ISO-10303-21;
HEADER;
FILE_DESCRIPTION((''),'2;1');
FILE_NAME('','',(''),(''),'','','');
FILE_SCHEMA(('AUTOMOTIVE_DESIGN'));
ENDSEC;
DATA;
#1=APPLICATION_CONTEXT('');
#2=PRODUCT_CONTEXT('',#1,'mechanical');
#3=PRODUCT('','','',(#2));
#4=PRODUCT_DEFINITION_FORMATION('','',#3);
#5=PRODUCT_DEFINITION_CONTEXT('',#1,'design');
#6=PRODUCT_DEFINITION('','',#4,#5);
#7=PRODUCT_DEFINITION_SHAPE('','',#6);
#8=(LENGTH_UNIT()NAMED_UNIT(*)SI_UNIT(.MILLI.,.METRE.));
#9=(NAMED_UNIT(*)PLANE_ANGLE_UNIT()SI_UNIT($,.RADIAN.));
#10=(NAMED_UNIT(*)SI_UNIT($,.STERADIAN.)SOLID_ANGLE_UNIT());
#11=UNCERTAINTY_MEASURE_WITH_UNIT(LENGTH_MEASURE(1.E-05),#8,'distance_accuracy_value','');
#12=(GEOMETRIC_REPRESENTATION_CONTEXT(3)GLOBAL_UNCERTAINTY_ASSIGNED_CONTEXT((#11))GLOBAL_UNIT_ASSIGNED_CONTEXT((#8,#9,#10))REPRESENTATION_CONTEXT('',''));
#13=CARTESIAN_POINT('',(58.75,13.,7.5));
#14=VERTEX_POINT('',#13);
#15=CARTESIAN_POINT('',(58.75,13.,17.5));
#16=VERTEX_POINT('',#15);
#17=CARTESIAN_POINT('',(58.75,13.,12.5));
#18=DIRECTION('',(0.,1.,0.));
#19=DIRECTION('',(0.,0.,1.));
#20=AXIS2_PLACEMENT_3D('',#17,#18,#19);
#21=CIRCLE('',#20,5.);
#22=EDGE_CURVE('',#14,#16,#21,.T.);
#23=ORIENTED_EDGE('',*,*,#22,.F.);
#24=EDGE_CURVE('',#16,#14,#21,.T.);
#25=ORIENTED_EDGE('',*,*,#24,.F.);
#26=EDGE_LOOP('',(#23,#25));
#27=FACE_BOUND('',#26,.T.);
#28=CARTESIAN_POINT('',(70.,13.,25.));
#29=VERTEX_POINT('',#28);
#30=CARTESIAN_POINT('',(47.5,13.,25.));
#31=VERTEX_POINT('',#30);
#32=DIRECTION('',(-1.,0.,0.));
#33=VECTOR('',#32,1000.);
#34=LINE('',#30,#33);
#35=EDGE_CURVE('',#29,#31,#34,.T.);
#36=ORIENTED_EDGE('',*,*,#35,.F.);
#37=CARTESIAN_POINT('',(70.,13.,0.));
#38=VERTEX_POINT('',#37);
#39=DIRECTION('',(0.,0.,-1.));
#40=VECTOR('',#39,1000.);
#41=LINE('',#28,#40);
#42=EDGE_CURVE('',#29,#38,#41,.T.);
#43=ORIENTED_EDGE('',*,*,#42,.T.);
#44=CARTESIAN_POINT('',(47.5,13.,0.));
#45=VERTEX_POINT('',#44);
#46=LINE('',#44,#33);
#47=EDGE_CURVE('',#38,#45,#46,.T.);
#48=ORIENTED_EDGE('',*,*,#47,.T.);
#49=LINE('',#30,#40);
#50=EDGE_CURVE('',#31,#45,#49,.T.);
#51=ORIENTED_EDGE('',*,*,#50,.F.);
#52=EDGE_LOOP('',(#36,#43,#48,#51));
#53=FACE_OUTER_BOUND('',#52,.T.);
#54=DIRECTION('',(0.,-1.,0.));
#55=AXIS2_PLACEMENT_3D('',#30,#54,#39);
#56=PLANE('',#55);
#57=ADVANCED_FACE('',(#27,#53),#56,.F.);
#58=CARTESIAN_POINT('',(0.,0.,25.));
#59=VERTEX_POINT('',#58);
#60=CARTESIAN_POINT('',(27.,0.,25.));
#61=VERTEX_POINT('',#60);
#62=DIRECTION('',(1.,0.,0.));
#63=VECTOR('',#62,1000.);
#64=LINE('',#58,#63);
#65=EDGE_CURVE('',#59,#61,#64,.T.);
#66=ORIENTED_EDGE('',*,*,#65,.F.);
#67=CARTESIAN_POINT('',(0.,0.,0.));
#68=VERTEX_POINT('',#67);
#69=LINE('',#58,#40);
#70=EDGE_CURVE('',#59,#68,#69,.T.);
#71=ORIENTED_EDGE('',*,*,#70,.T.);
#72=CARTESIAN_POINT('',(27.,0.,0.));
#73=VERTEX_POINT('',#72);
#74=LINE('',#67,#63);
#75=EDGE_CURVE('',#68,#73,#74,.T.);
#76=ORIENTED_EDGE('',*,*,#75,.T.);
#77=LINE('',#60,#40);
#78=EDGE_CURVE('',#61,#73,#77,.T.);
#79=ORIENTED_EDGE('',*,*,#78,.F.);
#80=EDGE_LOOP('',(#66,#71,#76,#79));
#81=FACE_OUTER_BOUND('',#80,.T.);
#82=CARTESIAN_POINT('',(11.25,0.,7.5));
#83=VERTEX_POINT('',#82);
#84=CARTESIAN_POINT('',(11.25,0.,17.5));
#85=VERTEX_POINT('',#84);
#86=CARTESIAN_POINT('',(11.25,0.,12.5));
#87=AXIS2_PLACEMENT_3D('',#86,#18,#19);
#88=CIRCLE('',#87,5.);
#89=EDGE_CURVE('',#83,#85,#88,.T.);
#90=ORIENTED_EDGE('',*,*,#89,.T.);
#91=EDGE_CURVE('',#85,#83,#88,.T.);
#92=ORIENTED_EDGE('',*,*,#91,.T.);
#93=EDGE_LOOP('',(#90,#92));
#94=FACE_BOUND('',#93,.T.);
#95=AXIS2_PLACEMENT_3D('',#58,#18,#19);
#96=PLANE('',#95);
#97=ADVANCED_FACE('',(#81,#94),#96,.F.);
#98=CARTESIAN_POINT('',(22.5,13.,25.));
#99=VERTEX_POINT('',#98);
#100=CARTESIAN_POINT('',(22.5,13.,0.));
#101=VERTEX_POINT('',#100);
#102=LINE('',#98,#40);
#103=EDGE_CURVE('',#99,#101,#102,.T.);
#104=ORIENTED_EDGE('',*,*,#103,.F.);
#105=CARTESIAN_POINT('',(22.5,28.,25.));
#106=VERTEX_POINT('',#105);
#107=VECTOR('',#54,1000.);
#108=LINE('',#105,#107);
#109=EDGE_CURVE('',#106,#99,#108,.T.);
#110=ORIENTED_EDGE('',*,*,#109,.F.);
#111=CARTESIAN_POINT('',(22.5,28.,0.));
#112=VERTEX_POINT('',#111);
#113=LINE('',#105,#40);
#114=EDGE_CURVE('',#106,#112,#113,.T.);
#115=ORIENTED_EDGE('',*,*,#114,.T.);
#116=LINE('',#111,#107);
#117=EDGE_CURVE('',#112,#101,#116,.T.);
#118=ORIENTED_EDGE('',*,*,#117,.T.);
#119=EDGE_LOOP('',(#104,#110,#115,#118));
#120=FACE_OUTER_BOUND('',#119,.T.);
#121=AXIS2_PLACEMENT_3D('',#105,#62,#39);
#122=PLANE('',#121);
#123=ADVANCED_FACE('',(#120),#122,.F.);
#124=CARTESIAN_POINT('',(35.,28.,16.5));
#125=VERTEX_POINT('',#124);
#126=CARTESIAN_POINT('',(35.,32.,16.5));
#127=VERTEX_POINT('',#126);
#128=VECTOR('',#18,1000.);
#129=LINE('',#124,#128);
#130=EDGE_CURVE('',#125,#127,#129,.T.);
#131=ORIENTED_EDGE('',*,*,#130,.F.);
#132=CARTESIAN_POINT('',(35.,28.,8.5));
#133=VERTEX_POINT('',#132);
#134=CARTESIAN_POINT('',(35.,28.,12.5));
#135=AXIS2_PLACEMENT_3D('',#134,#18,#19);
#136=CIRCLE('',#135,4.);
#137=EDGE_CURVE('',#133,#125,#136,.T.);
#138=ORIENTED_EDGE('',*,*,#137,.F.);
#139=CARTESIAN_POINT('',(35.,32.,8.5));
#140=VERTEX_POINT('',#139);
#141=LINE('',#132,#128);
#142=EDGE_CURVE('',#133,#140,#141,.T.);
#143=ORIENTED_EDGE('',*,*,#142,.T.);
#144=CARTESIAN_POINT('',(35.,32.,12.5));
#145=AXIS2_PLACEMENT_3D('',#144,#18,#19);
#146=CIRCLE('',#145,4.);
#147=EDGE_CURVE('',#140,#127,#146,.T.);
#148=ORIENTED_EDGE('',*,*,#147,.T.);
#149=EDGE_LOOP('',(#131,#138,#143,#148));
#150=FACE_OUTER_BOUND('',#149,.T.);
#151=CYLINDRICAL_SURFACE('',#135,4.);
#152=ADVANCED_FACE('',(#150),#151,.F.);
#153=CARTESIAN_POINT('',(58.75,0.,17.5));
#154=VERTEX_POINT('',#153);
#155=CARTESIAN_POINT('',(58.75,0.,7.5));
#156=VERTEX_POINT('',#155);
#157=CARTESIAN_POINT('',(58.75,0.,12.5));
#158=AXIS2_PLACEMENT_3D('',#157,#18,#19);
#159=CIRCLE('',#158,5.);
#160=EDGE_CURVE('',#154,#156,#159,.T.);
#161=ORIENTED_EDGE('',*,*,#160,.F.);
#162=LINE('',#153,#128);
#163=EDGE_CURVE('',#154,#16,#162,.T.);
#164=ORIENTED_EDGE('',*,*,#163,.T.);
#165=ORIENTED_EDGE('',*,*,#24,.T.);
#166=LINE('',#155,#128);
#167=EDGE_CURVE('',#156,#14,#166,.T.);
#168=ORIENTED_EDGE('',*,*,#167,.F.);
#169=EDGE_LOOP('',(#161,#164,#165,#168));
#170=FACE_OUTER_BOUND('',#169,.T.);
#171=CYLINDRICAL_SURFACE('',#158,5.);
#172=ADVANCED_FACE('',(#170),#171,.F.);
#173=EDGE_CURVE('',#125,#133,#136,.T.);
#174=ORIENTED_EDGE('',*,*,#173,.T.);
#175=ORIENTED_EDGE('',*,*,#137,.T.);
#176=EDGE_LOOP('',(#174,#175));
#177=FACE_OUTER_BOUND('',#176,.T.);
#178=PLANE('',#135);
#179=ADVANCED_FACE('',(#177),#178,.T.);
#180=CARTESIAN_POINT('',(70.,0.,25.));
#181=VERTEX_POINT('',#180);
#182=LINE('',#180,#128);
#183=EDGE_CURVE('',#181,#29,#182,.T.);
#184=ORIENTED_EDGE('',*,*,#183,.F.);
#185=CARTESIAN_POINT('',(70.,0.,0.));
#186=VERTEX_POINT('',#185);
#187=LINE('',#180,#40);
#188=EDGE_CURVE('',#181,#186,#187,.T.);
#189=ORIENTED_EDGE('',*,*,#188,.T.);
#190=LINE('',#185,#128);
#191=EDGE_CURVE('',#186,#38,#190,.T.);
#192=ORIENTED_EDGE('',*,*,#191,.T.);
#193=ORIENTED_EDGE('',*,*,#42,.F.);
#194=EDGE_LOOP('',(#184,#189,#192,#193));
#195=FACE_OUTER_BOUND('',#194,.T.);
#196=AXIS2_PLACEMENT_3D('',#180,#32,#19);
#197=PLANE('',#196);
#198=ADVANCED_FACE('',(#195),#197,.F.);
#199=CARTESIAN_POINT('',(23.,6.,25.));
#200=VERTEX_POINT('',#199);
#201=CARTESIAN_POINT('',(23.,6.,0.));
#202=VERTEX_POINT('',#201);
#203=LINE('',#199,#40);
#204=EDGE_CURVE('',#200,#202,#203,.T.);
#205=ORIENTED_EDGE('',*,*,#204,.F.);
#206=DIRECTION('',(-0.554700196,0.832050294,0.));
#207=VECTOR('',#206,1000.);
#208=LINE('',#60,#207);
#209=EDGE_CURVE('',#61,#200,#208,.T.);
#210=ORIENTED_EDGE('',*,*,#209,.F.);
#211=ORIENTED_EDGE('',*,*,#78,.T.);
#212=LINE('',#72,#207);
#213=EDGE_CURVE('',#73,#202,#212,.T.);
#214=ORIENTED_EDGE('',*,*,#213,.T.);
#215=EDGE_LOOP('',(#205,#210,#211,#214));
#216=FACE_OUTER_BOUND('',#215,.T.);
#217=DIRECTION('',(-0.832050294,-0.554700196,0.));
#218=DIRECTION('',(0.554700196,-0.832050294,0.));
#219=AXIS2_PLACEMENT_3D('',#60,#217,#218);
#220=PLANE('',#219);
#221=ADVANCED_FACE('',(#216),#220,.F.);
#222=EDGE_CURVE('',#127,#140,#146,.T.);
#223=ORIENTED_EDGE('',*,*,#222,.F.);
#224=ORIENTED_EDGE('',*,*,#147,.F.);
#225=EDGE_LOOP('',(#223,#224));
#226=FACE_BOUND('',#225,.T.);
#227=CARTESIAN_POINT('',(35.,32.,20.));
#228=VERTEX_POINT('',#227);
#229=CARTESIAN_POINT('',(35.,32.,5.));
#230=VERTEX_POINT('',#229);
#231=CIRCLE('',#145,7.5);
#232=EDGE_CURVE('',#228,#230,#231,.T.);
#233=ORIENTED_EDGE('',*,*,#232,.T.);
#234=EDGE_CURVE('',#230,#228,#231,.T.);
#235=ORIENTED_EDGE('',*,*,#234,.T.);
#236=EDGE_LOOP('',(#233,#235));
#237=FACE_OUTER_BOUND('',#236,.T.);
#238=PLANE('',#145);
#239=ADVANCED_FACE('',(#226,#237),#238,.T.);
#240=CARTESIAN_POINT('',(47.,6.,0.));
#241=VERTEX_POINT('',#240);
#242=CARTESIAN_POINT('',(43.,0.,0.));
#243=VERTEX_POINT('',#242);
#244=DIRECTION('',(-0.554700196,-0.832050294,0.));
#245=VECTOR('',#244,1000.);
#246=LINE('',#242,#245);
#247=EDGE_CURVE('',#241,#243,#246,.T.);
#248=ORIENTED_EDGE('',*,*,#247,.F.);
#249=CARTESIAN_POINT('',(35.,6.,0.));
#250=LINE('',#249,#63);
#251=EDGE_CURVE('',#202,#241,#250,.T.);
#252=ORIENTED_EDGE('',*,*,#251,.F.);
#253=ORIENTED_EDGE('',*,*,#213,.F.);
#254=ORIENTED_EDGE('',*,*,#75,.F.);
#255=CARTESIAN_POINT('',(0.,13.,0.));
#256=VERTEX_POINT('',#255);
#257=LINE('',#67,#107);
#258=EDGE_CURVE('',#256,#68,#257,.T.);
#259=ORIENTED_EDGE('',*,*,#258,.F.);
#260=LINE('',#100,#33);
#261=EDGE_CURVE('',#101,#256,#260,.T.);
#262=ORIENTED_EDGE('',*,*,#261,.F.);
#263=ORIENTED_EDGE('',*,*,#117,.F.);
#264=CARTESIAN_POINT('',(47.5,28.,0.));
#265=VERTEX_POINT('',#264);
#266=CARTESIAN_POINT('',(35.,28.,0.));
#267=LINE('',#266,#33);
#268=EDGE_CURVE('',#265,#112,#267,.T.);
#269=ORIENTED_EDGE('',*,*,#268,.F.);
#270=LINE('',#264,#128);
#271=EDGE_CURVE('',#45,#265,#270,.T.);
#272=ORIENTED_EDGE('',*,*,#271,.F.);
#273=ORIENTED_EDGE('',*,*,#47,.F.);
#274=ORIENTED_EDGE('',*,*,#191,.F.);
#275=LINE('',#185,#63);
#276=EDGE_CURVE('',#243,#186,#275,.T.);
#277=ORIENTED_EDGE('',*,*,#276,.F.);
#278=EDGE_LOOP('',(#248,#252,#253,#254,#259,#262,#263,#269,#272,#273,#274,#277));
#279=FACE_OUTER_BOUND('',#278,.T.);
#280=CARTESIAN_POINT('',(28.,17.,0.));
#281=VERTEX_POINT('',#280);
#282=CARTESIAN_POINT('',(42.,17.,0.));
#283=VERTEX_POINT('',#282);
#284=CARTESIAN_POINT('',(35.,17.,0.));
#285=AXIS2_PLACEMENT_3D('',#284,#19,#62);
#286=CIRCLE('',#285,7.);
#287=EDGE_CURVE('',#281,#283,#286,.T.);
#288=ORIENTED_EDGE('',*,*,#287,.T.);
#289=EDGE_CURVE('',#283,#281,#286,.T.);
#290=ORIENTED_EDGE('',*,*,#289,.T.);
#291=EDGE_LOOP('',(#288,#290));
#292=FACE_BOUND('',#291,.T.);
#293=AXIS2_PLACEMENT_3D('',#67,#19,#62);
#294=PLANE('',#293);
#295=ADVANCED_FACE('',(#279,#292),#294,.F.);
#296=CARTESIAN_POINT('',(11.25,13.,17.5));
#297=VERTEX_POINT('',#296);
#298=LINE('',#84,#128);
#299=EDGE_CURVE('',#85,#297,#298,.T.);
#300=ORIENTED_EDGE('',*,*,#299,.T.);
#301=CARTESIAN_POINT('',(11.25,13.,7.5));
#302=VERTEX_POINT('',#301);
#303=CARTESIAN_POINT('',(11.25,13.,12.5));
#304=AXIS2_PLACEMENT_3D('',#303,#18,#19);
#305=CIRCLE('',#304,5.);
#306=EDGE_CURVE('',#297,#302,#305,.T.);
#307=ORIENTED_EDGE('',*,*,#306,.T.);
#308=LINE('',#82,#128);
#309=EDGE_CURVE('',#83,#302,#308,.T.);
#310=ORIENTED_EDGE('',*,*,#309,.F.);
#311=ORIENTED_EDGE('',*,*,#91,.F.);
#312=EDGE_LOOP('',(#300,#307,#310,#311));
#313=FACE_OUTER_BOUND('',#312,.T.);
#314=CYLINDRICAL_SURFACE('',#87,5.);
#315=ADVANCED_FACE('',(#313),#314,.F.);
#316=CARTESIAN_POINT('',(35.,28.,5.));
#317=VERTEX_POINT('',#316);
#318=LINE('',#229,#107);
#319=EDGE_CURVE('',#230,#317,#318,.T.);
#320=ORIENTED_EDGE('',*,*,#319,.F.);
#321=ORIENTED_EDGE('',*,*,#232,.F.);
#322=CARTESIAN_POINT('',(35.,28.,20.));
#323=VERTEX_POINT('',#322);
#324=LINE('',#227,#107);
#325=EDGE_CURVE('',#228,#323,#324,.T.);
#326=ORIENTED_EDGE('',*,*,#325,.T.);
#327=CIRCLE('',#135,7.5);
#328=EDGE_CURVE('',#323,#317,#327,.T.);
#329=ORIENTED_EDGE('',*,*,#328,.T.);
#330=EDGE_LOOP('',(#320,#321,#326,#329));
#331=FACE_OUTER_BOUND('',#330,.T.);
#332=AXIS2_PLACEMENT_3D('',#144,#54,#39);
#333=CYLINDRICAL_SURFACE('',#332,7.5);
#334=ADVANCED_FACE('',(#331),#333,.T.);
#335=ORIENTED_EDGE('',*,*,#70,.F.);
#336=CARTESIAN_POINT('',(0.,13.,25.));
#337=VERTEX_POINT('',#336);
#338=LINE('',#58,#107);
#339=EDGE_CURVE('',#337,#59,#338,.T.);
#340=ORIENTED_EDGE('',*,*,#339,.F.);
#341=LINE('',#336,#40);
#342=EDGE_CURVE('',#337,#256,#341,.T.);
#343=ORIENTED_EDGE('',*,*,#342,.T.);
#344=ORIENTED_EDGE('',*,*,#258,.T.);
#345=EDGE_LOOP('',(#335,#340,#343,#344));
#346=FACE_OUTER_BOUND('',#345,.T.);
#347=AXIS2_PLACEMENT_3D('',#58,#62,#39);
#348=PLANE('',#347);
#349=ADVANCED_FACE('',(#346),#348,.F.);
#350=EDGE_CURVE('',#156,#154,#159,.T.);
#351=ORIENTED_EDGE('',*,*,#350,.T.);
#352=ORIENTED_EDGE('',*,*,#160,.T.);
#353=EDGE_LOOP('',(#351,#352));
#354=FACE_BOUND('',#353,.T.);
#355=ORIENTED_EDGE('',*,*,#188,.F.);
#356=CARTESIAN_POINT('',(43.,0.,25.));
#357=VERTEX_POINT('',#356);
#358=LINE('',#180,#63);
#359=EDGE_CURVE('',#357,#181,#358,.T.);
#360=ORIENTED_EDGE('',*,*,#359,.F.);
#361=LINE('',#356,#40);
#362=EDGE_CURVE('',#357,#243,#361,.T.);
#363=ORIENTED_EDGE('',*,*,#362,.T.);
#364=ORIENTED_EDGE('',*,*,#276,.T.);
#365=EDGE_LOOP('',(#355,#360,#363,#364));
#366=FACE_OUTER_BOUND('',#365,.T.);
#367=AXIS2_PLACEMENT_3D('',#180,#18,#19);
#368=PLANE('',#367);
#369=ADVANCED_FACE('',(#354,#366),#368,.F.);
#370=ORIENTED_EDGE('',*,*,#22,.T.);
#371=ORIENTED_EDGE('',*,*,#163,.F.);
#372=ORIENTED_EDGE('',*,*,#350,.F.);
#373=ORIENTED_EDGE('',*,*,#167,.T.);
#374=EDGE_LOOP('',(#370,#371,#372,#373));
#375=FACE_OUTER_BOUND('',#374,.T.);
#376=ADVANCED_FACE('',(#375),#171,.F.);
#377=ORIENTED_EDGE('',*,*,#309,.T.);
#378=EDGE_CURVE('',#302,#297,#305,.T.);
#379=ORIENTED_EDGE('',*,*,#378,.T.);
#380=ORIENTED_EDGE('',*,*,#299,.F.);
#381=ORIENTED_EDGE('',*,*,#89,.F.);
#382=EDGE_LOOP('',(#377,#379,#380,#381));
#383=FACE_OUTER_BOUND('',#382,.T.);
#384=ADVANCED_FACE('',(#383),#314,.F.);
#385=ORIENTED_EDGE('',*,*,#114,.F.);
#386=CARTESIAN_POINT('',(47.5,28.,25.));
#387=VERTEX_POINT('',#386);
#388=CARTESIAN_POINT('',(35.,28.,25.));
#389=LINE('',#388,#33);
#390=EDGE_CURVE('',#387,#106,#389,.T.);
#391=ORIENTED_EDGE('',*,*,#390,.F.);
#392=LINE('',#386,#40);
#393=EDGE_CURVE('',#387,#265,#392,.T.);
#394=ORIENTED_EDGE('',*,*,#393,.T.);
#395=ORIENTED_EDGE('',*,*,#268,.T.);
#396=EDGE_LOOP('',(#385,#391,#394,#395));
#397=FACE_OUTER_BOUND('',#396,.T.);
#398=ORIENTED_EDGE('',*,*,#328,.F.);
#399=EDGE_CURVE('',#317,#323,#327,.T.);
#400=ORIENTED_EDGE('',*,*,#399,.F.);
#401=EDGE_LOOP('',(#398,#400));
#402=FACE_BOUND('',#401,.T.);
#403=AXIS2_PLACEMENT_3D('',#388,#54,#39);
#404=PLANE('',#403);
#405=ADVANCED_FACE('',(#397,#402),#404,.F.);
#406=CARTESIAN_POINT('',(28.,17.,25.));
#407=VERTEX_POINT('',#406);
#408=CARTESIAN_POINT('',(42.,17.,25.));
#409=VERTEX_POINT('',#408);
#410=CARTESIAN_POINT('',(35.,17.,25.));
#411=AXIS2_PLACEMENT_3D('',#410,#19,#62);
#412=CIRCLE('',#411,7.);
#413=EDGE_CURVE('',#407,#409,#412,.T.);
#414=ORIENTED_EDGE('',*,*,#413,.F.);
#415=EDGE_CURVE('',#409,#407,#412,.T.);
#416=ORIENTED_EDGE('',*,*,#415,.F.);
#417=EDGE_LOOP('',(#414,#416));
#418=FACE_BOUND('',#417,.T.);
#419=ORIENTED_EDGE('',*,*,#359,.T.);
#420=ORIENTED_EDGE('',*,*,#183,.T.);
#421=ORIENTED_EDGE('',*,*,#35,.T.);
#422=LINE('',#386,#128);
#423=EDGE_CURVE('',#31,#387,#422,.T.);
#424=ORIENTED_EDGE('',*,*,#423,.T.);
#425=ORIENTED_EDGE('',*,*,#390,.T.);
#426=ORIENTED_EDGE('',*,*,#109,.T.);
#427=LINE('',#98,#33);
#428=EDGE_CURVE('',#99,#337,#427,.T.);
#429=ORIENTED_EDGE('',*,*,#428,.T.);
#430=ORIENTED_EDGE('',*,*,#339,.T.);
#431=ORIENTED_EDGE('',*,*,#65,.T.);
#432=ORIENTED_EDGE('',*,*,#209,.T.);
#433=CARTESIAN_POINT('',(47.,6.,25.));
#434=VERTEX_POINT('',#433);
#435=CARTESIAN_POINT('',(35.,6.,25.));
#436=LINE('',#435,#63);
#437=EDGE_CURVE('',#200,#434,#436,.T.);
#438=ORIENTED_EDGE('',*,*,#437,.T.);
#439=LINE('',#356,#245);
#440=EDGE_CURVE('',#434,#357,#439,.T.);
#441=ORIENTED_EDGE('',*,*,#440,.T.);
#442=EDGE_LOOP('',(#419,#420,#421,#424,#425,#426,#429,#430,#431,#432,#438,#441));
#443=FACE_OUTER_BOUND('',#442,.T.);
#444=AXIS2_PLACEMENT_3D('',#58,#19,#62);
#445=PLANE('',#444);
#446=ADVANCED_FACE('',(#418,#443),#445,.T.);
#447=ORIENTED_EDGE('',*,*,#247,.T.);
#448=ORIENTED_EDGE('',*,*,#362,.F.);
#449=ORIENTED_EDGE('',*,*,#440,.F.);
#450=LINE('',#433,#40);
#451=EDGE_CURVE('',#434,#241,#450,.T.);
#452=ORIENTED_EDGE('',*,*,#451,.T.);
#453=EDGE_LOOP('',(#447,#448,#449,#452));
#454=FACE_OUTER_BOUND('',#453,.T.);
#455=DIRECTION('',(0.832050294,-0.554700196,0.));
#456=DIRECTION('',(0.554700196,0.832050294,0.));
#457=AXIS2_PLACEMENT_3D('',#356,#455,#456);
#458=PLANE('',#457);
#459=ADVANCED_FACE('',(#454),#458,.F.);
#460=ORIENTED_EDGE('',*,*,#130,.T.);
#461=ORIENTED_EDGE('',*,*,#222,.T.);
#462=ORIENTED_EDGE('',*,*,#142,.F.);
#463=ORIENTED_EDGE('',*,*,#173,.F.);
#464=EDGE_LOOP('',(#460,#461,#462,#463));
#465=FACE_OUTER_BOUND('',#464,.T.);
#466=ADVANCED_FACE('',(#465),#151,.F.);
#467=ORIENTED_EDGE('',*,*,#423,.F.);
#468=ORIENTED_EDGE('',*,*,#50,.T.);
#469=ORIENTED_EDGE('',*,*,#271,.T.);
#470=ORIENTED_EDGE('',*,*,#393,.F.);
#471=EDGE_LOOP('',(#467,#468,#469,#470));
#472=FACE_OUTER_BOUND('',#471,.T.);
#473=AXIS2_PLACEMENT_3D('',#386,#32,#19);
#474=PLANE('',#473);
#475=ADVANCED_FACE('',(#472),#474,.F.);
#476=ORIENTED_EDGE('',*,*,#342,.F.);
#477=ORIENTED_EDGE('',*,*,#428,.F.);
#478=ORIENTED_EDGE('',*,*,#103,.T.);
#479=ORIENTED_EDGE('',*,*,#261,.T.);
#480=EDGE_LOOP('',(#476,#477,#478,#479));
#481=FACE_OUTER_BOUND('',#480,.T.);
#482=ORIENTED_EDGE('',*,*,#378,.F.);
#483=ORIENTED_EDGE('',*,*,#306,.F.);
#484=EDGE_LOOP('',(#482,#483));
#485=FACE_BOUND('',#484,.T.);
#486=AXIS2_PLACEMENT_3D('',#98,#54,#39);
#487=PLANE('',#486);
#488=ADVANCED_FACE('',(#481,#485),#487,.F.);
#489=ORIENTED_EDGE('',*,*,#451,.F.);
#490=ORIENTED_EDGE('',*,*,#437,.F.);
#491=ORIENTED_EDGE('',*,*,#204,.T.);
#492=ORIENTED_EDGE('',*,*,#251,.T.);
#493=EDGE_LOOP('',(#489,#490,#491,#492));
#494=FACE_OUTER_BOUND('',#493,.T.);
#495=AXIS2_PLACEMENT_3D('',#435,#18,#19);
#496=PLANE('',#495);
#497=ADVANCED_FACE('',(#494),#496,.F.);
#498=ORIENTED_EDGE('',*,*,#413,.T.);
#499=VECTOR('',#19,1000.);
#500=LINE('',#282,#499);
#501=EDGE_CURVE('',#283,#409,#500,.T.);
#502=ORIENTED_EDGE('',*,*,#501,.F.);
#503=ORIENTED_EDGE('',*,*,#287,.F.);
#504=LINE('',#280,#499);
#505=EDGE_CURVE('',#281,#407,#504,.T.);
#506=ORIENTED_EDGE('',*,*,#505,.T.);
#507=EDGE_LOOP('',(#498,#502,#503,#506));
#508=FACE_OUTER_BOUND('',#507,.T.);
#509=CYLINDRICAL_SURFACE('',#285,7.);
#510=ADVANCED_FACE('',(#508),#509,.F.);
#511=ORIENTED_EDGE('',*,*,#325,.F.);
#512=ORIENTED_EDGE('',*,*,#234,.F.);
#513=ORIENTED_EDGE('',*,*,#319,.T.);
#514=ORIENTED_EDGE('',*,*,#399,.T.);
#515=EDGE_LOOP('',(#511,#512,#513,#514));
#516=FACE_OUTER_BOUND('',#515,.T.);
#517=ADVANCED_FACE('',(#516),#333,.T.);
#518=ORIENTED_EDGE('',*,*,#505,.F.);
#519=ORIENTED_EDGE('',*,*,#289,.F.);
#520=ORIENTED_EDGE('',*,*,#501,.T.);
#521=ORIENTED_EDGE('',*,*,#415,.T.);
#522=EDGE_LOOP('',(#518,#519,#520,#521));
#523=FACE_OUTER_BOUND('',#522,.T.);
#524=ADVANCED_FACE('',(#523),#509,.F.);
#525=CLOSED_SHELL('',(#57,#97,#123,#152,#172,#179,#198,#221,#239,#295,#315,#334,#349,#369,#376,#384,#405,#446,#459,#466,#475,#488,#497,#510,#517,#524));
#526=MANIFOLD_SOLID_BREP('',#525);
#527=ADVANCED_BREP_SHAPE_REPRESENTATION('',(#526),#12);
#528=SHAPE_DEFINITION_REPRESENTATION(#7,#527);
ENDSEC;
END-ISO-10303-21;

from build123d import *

# Parameters (mm, degrees)
STEPPED_BLOCK_DEPTH          = 25
CROSS_HOLE_SKETCH_R          = 7
CROSS_HOLE_11_DEPTH          = 25
STEP_HOLES_SKETCH_R          = 5
STEP_HOLES_2X_DEPTH_13_DEPTH = 13
TOP_BOSS_SKETCH_R            = 7.5
TOP_BOSS_DEPTH               = 4
TOP_BOSS_BORE_SKETCH_R       = 4
TOP_BOSS_BORE_DEPTH          = 4


with BuildPart() as part:
    # Stepped Block Profile → Stepped Block (new body)
    with BuildSketch(Plane.XY):
        Polygon((0, 0), (0, 13), (22.5, 13), (22.5, 28), (35, 28), (47.5, 28), (47.5, 13), (70, 13), (70, 0), (43, 0), (47, 6), (35, 6), (23, 6), (27, 0), align=None)
    extrude(amount=STEPPED_BLOCK_DEPTH)

    # Cross Hole Sketch → Cross Hole Ø11 (cut)
    with BuildSketch(Plane.XY.offset(25)):
        with Locations((35, 17)):
            Circle(CROSS_HOLE_SKETCH_R)
    extrude(amount=-CROSS_HOLE_11_DEPTH, mode=Mode.SUBTRACT)

    # Step Holes Sketch → Step Holes 2x Depth 13 (cut)
    with BuildSketch(Plane(origin=(0, 13, 0), x_dir=(1, 0, 0), z_dir=(0, 1, 0))):
        with Locations(Location((58.75, -12.5, 0), (0, 0, 270))):
            Circle(STEP_HOLES_SKETCH_R)
        with Locations(Location((11.25, -12.5, 0), (0, 0, 270))):
            Circle(STEP_HOLES_SKETCH_R)
    extrude(amount=-STEP_HOLES_2X_DEPTH_13_DEPTH, mode=Mode.SUBTRACT)

    # Top Boss Sketch → Top Boss (add)
    with BuildSketch(Plane(origin=(0, 28, 0), x_dir=(1, 0, 0), z_dir=(0, 1, 0))):
        with Locations(Location((35, -12.5, 0), (0, 0, 270))):
            Circle(TOP_BOSS_SKETCH_R)
    extrude(amount=TOP_BOSS_DEPTH)

    # Top Boss Bore Sketch → Top Boss Bore (cut)
    with BuildSketch(Plane(origin=(0, 32, 0), x_dir=(1, 0, 0), z_dir=(0, 1, 0))):
        with Locations(Location((35, -12.5, 0), (0, 0, 270))):
            Circle(TOP_BOSS_BORE_SKETCH_R)
    extrude(amount=-TOP_BOSS_BORE_DEPTH, mode=Mode.SUBTRACT)


solid = part.part
